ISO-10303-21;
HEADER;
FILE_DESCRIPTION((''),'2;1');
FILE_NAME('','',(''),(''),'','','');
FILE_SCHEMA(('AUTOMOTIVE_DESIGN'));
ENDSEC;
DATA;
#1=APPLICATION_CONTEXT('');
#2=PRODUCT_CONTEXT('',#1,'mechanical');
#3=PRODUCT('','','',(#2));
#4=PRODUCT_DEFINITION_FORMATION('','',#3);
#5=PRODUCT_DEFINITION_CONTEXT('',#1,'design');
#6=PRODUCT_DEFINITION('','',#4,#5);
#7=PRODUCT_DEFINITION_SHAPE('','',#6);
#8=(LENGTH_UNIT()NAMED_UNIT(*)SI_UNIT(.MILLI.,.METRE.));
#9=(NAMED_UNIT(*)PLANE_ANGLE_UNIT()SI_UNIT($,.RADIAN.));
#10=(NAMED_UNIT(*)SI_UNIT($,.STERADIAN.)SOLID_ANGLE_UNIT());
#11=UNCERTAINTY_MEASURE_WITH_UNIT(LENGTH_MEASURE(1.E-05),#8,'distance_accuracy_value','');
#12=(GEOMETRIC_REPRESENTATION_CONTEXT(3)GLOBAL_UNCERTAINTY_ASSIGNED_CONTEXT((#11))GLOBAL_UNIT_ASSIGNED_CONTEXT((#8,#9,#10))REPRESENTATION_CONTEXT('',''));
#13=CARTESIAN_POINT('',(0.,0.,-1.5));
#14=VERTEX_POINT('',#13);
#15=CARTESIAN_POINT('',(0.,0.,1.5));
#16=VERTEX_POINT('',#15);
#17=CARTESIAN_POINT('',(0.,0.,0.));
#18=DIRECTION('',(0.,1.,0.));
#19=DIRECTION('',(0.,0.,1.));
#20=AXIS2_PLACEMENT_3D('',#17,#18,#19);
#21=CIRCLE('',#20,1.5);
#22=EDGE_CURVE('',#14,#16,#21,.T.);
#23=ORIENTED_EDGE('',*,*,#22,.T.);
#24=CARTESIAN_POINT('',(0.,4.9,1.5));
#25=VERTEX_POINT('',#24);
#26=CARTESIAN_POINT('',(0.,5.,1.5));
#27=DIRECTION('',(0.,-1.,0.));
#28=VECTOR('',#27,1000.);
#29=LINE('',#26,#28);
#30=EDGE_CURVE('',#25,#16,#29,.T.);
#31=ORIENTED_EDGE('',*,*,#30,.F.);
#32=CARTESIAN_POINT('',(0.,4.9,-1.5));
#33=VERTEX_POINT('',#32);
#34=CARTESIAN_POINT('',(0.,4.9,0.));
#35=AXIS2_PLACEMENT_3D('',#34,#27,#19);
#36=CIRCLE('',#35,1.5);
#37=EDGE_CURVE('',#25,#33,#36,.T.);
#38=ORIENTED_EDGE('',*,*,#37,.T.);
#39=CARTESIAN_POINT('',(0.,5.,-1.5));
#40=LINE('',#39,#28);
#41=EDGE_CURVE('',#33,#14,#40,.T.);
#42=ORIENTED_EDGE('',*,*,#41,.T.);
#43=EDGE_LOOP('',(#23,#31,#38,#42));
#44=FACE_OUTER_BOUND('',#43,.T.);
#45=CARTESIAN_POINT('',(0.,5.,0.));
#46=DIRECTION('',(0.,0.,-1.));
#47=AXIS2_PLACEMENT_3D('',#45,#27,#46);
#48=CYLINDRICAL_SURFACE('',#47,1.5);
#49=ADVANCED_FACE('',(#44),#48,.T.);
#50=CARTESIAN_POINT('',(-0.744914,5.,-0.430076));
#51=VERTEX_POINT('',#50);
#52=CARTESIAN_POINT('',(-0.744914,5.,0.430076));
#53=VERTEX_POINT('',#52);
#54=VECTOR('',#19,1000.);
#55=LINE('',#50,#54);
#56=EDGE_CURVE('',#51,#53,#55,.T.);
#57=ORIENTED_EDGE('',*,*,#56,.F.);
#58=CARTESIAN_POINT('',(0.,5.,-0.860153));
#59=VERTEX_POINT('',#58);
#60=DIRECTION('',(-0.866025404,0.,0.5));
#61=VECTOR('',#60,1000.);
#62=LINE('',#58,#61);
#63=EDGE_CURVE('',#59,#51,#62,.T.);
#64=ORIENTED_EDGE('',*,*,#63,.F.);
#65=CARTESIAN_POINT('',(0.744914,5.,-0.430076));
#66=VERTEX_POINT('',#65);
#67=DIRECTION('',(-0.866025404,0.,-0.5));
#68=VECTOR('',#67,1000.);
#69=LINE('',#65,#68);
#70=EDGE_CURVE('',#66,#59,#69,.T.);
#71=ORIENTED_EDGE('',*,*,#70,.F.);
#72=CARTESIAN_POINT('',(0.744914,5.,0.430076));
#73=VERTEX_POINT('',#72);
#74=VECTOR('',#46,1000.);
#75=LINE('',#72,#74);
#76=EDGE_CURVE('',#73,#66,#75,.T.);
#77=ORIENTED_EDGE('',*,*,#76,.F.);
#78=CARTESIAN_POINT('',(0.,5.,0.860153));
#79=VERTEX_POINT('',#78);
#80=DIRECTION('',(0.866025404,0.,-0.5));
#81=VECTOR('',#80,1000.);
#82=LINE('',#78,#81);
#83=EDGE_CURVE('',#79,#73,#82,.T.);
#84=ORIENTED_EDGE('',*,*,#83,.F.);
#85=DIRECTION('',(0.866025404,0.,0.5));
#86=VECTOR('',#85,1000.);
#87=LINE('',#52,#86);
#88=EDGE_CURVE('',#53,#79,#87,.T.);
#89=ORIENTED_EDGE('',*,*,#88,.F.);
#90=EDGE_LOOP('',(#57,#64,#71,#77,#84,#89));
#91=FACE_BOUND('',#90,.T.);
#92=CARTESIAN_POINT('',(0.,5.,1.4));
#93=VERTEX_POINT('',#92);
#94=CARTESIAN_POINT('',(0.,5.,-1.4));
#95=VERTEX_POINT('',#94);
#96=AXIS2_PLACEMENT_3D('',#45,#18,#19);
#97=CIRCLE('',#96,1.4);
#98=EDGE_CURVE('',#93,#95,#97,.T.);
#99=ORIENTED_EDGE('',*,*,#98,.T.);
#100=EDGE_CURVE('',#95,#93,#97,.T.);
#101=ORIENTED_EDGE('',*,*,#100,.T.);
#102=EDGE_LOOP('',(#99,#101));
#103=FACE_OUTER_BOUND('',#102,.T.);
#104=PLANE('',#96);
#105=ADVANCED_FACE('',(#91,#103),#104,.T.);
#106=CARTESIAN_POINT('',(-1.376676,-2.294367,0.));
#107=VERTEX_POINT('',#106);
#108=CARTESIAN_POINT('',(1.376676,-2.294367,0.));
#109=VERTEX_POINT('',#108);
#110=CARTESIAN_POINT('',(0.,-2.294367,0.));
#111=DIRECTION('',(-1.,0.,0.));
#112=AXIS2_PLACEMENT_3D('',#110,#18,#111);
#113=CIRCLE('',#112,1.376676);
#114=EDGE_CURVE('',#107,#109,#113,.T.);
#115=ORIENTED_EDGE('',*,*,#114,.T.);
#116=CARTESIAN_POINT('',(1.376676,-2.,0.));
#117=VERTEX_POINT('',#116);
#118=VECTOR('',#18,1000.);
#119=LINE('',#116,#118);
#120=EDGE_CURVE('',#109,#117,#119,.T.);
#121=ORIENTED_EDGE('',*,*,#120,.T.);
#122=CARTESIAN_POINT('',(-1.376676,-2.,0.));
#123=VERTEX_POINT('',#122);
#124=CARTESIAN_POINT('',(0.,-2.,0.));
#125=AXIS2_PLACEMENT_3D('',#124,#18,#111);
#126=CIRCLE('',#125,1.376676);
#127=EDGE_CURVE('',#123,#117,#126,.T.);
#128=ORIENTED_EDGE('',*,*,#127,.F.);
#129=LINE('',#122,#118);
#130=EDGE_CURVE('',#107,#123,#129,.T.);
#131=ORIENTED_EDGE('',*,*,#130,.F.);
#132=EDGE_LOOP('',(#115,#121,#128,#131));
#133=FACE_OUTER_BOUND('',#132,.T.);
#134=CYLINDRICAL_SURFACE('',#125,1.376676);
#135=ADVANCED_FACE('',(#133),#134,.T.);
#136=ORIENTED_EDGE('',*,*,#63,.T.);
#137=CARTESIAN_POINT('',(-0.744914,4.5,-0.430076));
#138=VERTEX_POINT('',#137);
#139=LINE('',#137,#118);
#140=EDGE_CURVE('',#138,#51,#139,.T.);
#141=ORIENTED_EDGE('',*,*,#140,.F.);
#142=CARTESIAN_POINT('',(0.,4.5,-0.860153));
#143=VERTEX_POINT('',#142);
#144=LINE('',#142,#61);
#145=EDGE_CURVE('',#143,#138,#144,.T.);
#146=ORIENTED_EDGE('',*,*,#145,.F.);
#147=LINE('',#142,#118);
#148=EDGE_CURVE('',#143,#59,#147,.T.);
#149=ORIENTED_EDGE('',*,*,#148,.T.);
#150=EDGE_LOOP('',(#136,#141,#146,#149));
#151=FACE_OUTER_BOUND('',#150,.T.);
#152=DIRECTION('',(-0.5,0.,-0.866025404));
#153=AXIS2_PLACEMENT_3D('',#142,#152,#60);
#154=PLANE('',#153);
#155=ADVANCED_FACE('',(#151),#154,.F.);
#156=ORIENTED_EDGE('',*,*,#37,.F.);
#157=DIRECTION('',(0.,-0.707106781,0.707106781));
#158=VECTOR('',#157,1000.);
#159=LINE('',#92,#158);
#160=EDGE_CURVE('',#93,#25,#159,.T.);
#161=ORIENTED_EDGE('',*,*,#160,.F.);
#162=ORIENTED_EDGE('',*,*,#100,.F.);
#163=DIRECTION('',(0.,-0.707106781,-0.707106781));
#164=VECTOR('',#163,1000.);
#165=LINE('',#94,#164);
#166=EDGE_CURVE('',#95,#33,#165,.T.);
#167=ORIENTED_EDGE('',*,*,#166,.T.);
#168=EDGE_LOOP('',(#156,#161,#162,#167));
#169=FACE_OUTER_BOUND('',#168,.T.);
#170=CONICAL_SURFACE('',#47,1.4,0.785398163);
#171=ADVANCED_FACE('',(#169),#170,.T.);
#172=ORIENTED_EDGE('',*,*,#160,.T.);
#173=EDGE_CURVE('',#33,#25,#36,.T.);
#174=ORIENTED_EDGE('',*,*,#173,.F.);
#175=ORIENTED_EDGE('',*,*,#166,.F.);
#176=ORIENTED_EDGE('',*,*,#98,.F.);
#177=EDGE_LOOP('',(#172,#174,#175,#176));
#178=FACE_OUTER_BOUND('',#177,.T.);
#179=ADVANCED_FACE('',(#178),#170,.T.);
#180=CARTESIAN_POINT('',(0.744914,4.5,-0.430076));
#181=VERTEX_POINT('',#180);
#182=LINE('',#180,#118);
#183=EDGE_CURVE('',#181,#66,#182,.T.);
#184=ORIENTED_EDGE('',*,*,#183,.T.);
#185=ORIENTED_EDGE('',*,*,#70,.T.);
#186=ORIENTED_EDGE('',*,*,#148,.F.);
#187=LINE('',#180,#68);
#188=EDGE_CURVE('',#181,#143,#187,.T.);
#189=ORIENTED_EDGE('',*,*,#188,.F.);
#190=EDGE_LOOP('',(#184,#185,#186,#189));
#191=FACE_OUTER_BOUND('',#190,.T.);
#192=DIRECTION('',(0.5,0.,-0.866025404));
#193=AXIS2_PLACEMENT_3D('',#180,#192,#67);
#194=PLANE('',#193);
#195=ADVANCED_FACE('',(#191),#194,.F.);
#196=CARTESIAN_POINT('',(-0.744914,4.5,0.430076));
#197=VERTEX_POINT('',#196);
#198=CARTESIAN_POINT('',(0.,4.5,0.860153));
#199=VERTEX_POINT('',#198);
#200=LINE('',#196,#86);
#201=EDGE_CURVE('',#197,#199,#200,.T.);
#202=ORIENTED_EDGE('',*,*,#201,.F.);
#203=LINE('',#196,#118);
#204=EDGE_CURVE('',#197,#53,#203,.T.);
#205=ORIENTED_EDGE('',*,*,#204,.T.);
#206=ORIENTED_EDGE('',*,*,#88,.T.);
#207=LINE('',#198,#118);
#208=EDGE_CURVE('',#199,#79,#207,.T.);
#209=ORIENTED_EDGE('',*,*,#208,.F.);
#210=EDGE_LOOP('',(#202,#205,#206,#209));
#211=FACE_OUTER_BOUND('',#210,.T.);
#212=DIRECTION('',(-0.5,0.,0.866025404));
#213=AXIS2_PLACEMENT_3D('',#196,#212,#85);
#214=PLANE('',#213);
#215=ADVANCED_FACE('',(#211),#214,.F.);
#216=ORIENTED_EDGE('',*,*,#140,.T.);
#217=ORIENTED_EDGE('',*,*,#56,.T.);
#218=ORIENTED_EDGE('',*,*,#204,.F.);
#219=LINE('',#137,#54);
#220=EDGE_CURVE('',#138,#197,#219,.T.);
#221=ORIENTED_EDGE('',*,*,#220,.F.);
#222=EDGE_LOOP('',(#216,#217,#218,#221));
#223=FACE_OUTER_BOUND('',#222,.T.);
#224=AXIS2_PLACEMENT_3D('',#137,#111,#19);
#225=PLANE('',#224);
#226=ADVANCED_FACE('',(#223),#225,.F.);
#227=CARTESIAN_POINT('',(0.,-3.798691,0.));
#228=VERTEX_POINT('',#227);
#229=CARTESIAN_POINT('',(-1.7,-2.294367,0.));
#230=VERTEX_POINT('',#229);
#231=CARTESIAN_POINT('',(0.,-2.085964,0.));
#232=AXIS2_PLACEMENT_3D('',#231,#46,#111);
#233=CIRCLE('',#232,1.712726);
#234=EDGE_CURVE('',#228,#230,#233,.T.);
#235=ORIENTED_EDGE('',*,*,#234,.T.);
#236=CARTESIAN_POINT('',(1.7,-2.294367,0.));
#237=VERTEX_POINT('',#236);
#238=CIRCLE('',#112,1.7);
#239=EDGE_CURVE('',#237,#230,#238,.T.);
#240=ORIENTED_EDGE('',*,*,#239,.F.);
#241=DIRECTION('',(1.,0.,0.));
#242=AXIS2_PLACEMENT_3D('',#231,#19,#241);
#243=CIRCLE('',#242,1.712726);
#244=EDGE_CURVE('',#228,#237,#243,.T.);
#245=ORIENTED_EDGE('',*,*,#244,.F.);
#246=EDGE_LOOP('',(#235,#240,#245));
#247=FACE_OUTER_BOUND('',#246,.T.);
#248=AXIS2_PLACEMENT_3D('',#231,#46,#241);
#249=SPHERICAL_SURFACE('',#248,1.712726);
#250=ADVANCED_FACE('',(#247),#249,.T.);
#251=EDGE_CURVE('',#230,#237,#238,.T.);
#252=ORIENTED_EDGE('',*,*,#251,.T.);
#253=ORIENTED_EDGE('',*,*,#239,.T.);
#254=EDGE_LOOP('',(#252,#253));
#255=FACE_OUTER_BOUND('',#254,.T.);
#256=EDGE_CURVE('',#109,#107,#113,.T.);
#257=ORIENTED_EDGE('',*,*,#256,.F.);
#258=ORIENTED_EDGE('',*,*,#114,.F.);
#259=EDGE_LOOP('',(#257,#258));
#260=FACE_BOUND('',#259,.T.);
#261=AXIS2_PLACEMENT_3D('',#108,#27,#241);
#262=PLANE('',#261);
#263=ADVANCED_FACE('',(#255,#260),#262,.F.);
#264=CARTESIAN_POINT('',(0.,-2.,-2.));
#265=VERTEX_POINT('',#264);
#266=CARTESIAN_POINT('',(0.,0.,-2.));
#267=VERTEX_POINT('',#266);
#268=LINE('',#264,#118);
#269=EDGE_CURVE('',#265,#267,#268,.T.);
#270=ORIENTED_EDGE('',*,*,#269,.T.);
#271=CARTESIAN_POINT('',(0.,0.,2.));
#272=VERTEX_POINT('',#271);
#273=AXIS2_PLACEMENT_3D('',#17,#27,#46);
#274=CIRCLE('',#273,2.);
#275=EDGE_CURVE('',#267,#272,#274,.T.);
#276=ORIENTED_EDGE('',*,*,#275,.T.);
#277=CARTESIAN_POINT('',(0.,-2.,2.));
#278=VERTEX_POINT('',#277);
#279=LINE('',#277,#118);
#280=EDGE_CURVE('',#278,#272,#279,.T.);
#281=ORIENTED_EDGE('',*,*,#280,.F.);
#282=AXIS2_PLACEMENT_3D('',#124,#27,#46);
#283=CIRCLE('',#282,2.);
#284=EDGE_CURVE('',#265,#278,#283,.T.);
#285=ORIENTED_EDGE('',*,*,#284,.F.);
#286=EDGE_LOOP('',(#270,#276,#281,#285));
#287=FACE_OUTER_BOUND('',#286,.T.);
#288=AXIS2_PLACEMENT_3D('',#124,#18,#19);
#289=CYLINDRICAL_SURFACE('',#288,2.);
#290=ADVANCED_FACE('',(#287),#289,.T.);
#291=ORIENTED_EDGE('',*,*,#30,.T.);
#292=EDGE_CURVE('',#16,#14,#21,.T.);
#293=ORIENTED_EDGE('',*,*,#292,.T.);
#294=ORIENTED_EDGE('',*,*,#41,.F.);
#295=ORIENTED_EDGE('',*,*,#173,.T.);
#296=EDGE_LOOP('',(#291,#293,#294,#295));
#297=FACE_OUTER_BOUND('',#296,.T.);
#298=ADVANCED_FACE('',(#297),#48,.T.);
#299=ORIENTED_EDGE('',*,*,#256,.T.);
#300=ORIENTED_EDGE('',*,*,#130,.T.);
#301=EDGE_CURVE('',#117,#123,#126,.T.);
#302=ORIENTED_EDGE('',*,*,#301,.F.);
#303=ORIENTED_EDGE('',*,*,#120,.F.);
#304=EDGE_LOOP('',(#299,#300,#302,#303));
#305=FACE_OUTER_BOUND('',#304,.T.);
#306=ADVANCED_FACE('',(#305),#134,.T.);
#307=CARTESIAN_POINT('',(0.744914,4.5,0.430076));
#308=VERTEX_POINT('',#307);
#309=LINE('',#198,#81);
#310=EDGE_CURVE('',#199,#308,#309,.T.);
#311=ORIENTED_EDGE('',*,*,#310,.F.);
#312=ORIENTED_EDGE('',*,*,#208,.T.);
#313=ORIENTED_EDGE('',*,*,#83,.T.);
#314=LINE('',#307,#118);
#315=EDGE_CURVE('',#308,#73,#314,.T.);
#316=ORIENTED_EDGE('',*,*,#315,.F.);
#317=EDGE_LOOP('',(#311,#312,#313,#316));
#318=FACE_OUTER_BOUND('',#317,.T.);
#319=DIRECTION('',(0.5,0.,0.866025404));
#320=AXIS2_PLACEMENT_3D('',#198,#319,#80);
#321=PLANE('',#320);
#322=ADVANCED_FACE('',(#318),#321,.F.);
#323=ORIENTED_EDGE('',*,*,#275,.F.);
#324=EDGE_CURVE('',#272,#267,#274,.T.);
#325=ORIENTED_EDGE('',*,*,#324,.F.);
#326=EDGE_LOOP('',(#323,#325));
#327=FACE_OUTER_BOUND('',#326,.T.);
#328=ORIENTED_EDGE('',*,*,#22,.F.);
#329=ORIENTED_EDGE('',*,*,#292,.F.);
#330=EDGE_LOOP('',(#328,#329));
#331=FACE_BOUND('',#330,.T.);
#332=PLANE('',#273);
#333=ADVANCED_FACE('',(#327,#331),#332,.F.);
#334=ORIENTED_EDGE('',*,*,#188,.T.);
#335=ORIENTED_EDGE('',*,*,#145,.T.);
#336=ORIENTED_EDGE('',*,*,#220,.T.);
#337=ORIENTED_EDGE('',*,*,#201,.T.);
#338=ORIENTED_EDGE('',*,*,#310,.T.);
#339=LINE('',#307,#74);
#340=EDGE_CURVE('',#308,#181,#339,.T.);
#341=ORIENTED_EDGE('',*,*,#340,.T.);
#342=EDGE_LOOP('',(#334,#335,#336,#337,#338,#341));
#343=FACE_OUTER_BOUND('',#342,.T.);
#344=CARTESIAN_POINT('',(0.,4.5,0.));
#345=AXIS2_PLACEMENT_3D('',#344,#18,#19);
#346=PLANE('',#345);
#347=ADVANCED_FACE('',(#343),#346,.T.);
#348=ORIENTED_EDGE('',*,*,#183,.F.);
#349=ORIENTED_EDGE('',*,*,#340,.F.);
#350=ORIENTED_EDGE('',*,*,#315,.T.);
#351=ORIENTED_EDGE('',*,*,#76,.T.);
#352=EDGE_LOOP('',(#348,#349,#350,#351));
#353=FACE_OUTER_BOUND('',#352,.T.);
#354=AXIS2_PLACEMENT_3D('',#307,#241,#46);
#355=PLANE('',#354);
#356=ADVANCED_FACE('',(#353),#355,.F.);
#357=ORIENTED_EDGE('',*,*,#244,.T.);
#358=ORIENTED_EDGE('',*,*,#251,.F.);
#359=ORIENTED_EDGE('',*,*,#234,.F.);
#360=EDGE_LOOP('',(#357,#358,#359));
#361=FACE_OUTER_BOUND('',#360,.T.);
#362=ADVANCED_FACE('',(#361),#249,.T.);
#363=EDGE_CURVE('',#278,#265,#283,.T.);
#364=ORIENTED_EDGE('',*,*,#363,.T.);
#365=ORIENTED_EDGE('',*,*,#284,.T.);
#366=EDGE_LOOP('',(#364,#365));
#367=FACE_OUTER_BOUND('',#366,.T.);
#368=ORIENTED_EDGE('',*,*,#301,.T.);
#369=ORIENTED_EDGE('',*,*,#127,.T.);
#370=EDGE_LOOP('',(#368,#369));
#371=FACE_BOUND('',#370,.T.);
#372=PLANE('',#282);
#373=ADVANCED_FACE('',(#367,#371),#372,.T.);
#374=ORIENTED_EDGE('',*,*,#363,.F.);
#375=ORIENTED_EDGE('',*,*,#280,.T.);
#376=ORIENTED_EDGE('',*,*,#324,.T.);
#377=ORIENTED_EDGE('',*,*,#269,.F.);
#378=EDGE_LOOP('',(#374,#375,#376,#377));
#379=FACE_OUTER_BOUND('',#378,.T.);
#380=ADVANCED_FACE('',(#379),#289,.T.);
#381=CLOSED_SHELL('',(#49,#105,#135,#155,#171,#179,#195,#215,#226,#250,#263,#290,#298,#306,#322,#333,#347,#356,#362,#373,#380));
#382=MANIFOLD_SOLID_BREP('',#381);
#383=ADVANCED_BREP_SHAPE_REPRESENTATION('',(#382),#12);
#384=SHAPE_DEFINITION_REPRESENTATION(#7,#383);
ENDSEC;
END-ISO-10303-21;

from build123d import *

# Parameters (mm, degrees)
SKETCH1_R           = 1.5
BOSS_EXTRUDE1_DEPTH = 5
SKETCH2_R           = 2
BOSS_EXTRUDE2_DEPTH = 2
CUT_EXTRUDE1_DEPTH  = 0.5
CHAMFER1_SIZE       = 0.1


with BuildPart() as part:
    # Sketch1 → Boss-Extrude1 (new body)
    with BuildSketch(Plane(origin=(0, 0, 0), x_dir=(1, 0, 0), z_dir=(0, 1, 0))):
        with Locations(Location((0, 0, 0), (0, 0, 270))):
            Circle(SKETCH1_R)
    extrude(amount=BOSS_EXTRUDE1_DEPTH)

    # Sketch2 → Boss-Extrude2 (add)
    with BuildSketch(Plane.XZ):
        with Locations(Location((0, 0, 0), (0, 0, 270))):
            Circle(SKETCH2_R)
    extrude(amount=BOSS_EXTRUDE2_DEPTH)

    # Sketch3 → Revolve1 (revolve)
    with BuildSketch(Plane.XY):
        with BuildLine():
            Line((0, -2), (0, -3.798690772))
            ThreePointArc((0, -3.798690772), (1.135010023, -3.368611599), (1.7, -2.294366668))
            Line((1.7, -2.294366668), (1.376675655, -2.294366668))
            Line((1.376675655, -2.294366668), (1.376675655, -2))
            Line((1.376675655, -2), (0, -2))
        make_face()
    revolve(axis=Axis((0, -2, 0), (0, -1, 0)))

    # Sketch4 → Cut-Extrude1 (cut)
    with BuildSketch(Plane(origin=(0, 5, 0), x_dir=(1, 0, 0), z_dir=(0, 1, 0))):
        Polygon((0, 0.860152501), (-0.744913917, 0.430076251), (-0.744913917, -0.430076251), (0, -0.860152501), (0.744913917, -0.430076251), (0.744913917, 0.430076251), align=None)
    extrude(amount=-CUT_EXTRUDE1_DEPTH, mode=Mode.SUBTRACT)

    # Chamfer1
    chamfer1_edges = [part.edges().sort_by_distance(p)[0] for p in [
        (0, 5, -1.5),
    ]]
    chamfer(chamfer1_edges, length=CHAMFER1_SIZE)


solid = part.part
